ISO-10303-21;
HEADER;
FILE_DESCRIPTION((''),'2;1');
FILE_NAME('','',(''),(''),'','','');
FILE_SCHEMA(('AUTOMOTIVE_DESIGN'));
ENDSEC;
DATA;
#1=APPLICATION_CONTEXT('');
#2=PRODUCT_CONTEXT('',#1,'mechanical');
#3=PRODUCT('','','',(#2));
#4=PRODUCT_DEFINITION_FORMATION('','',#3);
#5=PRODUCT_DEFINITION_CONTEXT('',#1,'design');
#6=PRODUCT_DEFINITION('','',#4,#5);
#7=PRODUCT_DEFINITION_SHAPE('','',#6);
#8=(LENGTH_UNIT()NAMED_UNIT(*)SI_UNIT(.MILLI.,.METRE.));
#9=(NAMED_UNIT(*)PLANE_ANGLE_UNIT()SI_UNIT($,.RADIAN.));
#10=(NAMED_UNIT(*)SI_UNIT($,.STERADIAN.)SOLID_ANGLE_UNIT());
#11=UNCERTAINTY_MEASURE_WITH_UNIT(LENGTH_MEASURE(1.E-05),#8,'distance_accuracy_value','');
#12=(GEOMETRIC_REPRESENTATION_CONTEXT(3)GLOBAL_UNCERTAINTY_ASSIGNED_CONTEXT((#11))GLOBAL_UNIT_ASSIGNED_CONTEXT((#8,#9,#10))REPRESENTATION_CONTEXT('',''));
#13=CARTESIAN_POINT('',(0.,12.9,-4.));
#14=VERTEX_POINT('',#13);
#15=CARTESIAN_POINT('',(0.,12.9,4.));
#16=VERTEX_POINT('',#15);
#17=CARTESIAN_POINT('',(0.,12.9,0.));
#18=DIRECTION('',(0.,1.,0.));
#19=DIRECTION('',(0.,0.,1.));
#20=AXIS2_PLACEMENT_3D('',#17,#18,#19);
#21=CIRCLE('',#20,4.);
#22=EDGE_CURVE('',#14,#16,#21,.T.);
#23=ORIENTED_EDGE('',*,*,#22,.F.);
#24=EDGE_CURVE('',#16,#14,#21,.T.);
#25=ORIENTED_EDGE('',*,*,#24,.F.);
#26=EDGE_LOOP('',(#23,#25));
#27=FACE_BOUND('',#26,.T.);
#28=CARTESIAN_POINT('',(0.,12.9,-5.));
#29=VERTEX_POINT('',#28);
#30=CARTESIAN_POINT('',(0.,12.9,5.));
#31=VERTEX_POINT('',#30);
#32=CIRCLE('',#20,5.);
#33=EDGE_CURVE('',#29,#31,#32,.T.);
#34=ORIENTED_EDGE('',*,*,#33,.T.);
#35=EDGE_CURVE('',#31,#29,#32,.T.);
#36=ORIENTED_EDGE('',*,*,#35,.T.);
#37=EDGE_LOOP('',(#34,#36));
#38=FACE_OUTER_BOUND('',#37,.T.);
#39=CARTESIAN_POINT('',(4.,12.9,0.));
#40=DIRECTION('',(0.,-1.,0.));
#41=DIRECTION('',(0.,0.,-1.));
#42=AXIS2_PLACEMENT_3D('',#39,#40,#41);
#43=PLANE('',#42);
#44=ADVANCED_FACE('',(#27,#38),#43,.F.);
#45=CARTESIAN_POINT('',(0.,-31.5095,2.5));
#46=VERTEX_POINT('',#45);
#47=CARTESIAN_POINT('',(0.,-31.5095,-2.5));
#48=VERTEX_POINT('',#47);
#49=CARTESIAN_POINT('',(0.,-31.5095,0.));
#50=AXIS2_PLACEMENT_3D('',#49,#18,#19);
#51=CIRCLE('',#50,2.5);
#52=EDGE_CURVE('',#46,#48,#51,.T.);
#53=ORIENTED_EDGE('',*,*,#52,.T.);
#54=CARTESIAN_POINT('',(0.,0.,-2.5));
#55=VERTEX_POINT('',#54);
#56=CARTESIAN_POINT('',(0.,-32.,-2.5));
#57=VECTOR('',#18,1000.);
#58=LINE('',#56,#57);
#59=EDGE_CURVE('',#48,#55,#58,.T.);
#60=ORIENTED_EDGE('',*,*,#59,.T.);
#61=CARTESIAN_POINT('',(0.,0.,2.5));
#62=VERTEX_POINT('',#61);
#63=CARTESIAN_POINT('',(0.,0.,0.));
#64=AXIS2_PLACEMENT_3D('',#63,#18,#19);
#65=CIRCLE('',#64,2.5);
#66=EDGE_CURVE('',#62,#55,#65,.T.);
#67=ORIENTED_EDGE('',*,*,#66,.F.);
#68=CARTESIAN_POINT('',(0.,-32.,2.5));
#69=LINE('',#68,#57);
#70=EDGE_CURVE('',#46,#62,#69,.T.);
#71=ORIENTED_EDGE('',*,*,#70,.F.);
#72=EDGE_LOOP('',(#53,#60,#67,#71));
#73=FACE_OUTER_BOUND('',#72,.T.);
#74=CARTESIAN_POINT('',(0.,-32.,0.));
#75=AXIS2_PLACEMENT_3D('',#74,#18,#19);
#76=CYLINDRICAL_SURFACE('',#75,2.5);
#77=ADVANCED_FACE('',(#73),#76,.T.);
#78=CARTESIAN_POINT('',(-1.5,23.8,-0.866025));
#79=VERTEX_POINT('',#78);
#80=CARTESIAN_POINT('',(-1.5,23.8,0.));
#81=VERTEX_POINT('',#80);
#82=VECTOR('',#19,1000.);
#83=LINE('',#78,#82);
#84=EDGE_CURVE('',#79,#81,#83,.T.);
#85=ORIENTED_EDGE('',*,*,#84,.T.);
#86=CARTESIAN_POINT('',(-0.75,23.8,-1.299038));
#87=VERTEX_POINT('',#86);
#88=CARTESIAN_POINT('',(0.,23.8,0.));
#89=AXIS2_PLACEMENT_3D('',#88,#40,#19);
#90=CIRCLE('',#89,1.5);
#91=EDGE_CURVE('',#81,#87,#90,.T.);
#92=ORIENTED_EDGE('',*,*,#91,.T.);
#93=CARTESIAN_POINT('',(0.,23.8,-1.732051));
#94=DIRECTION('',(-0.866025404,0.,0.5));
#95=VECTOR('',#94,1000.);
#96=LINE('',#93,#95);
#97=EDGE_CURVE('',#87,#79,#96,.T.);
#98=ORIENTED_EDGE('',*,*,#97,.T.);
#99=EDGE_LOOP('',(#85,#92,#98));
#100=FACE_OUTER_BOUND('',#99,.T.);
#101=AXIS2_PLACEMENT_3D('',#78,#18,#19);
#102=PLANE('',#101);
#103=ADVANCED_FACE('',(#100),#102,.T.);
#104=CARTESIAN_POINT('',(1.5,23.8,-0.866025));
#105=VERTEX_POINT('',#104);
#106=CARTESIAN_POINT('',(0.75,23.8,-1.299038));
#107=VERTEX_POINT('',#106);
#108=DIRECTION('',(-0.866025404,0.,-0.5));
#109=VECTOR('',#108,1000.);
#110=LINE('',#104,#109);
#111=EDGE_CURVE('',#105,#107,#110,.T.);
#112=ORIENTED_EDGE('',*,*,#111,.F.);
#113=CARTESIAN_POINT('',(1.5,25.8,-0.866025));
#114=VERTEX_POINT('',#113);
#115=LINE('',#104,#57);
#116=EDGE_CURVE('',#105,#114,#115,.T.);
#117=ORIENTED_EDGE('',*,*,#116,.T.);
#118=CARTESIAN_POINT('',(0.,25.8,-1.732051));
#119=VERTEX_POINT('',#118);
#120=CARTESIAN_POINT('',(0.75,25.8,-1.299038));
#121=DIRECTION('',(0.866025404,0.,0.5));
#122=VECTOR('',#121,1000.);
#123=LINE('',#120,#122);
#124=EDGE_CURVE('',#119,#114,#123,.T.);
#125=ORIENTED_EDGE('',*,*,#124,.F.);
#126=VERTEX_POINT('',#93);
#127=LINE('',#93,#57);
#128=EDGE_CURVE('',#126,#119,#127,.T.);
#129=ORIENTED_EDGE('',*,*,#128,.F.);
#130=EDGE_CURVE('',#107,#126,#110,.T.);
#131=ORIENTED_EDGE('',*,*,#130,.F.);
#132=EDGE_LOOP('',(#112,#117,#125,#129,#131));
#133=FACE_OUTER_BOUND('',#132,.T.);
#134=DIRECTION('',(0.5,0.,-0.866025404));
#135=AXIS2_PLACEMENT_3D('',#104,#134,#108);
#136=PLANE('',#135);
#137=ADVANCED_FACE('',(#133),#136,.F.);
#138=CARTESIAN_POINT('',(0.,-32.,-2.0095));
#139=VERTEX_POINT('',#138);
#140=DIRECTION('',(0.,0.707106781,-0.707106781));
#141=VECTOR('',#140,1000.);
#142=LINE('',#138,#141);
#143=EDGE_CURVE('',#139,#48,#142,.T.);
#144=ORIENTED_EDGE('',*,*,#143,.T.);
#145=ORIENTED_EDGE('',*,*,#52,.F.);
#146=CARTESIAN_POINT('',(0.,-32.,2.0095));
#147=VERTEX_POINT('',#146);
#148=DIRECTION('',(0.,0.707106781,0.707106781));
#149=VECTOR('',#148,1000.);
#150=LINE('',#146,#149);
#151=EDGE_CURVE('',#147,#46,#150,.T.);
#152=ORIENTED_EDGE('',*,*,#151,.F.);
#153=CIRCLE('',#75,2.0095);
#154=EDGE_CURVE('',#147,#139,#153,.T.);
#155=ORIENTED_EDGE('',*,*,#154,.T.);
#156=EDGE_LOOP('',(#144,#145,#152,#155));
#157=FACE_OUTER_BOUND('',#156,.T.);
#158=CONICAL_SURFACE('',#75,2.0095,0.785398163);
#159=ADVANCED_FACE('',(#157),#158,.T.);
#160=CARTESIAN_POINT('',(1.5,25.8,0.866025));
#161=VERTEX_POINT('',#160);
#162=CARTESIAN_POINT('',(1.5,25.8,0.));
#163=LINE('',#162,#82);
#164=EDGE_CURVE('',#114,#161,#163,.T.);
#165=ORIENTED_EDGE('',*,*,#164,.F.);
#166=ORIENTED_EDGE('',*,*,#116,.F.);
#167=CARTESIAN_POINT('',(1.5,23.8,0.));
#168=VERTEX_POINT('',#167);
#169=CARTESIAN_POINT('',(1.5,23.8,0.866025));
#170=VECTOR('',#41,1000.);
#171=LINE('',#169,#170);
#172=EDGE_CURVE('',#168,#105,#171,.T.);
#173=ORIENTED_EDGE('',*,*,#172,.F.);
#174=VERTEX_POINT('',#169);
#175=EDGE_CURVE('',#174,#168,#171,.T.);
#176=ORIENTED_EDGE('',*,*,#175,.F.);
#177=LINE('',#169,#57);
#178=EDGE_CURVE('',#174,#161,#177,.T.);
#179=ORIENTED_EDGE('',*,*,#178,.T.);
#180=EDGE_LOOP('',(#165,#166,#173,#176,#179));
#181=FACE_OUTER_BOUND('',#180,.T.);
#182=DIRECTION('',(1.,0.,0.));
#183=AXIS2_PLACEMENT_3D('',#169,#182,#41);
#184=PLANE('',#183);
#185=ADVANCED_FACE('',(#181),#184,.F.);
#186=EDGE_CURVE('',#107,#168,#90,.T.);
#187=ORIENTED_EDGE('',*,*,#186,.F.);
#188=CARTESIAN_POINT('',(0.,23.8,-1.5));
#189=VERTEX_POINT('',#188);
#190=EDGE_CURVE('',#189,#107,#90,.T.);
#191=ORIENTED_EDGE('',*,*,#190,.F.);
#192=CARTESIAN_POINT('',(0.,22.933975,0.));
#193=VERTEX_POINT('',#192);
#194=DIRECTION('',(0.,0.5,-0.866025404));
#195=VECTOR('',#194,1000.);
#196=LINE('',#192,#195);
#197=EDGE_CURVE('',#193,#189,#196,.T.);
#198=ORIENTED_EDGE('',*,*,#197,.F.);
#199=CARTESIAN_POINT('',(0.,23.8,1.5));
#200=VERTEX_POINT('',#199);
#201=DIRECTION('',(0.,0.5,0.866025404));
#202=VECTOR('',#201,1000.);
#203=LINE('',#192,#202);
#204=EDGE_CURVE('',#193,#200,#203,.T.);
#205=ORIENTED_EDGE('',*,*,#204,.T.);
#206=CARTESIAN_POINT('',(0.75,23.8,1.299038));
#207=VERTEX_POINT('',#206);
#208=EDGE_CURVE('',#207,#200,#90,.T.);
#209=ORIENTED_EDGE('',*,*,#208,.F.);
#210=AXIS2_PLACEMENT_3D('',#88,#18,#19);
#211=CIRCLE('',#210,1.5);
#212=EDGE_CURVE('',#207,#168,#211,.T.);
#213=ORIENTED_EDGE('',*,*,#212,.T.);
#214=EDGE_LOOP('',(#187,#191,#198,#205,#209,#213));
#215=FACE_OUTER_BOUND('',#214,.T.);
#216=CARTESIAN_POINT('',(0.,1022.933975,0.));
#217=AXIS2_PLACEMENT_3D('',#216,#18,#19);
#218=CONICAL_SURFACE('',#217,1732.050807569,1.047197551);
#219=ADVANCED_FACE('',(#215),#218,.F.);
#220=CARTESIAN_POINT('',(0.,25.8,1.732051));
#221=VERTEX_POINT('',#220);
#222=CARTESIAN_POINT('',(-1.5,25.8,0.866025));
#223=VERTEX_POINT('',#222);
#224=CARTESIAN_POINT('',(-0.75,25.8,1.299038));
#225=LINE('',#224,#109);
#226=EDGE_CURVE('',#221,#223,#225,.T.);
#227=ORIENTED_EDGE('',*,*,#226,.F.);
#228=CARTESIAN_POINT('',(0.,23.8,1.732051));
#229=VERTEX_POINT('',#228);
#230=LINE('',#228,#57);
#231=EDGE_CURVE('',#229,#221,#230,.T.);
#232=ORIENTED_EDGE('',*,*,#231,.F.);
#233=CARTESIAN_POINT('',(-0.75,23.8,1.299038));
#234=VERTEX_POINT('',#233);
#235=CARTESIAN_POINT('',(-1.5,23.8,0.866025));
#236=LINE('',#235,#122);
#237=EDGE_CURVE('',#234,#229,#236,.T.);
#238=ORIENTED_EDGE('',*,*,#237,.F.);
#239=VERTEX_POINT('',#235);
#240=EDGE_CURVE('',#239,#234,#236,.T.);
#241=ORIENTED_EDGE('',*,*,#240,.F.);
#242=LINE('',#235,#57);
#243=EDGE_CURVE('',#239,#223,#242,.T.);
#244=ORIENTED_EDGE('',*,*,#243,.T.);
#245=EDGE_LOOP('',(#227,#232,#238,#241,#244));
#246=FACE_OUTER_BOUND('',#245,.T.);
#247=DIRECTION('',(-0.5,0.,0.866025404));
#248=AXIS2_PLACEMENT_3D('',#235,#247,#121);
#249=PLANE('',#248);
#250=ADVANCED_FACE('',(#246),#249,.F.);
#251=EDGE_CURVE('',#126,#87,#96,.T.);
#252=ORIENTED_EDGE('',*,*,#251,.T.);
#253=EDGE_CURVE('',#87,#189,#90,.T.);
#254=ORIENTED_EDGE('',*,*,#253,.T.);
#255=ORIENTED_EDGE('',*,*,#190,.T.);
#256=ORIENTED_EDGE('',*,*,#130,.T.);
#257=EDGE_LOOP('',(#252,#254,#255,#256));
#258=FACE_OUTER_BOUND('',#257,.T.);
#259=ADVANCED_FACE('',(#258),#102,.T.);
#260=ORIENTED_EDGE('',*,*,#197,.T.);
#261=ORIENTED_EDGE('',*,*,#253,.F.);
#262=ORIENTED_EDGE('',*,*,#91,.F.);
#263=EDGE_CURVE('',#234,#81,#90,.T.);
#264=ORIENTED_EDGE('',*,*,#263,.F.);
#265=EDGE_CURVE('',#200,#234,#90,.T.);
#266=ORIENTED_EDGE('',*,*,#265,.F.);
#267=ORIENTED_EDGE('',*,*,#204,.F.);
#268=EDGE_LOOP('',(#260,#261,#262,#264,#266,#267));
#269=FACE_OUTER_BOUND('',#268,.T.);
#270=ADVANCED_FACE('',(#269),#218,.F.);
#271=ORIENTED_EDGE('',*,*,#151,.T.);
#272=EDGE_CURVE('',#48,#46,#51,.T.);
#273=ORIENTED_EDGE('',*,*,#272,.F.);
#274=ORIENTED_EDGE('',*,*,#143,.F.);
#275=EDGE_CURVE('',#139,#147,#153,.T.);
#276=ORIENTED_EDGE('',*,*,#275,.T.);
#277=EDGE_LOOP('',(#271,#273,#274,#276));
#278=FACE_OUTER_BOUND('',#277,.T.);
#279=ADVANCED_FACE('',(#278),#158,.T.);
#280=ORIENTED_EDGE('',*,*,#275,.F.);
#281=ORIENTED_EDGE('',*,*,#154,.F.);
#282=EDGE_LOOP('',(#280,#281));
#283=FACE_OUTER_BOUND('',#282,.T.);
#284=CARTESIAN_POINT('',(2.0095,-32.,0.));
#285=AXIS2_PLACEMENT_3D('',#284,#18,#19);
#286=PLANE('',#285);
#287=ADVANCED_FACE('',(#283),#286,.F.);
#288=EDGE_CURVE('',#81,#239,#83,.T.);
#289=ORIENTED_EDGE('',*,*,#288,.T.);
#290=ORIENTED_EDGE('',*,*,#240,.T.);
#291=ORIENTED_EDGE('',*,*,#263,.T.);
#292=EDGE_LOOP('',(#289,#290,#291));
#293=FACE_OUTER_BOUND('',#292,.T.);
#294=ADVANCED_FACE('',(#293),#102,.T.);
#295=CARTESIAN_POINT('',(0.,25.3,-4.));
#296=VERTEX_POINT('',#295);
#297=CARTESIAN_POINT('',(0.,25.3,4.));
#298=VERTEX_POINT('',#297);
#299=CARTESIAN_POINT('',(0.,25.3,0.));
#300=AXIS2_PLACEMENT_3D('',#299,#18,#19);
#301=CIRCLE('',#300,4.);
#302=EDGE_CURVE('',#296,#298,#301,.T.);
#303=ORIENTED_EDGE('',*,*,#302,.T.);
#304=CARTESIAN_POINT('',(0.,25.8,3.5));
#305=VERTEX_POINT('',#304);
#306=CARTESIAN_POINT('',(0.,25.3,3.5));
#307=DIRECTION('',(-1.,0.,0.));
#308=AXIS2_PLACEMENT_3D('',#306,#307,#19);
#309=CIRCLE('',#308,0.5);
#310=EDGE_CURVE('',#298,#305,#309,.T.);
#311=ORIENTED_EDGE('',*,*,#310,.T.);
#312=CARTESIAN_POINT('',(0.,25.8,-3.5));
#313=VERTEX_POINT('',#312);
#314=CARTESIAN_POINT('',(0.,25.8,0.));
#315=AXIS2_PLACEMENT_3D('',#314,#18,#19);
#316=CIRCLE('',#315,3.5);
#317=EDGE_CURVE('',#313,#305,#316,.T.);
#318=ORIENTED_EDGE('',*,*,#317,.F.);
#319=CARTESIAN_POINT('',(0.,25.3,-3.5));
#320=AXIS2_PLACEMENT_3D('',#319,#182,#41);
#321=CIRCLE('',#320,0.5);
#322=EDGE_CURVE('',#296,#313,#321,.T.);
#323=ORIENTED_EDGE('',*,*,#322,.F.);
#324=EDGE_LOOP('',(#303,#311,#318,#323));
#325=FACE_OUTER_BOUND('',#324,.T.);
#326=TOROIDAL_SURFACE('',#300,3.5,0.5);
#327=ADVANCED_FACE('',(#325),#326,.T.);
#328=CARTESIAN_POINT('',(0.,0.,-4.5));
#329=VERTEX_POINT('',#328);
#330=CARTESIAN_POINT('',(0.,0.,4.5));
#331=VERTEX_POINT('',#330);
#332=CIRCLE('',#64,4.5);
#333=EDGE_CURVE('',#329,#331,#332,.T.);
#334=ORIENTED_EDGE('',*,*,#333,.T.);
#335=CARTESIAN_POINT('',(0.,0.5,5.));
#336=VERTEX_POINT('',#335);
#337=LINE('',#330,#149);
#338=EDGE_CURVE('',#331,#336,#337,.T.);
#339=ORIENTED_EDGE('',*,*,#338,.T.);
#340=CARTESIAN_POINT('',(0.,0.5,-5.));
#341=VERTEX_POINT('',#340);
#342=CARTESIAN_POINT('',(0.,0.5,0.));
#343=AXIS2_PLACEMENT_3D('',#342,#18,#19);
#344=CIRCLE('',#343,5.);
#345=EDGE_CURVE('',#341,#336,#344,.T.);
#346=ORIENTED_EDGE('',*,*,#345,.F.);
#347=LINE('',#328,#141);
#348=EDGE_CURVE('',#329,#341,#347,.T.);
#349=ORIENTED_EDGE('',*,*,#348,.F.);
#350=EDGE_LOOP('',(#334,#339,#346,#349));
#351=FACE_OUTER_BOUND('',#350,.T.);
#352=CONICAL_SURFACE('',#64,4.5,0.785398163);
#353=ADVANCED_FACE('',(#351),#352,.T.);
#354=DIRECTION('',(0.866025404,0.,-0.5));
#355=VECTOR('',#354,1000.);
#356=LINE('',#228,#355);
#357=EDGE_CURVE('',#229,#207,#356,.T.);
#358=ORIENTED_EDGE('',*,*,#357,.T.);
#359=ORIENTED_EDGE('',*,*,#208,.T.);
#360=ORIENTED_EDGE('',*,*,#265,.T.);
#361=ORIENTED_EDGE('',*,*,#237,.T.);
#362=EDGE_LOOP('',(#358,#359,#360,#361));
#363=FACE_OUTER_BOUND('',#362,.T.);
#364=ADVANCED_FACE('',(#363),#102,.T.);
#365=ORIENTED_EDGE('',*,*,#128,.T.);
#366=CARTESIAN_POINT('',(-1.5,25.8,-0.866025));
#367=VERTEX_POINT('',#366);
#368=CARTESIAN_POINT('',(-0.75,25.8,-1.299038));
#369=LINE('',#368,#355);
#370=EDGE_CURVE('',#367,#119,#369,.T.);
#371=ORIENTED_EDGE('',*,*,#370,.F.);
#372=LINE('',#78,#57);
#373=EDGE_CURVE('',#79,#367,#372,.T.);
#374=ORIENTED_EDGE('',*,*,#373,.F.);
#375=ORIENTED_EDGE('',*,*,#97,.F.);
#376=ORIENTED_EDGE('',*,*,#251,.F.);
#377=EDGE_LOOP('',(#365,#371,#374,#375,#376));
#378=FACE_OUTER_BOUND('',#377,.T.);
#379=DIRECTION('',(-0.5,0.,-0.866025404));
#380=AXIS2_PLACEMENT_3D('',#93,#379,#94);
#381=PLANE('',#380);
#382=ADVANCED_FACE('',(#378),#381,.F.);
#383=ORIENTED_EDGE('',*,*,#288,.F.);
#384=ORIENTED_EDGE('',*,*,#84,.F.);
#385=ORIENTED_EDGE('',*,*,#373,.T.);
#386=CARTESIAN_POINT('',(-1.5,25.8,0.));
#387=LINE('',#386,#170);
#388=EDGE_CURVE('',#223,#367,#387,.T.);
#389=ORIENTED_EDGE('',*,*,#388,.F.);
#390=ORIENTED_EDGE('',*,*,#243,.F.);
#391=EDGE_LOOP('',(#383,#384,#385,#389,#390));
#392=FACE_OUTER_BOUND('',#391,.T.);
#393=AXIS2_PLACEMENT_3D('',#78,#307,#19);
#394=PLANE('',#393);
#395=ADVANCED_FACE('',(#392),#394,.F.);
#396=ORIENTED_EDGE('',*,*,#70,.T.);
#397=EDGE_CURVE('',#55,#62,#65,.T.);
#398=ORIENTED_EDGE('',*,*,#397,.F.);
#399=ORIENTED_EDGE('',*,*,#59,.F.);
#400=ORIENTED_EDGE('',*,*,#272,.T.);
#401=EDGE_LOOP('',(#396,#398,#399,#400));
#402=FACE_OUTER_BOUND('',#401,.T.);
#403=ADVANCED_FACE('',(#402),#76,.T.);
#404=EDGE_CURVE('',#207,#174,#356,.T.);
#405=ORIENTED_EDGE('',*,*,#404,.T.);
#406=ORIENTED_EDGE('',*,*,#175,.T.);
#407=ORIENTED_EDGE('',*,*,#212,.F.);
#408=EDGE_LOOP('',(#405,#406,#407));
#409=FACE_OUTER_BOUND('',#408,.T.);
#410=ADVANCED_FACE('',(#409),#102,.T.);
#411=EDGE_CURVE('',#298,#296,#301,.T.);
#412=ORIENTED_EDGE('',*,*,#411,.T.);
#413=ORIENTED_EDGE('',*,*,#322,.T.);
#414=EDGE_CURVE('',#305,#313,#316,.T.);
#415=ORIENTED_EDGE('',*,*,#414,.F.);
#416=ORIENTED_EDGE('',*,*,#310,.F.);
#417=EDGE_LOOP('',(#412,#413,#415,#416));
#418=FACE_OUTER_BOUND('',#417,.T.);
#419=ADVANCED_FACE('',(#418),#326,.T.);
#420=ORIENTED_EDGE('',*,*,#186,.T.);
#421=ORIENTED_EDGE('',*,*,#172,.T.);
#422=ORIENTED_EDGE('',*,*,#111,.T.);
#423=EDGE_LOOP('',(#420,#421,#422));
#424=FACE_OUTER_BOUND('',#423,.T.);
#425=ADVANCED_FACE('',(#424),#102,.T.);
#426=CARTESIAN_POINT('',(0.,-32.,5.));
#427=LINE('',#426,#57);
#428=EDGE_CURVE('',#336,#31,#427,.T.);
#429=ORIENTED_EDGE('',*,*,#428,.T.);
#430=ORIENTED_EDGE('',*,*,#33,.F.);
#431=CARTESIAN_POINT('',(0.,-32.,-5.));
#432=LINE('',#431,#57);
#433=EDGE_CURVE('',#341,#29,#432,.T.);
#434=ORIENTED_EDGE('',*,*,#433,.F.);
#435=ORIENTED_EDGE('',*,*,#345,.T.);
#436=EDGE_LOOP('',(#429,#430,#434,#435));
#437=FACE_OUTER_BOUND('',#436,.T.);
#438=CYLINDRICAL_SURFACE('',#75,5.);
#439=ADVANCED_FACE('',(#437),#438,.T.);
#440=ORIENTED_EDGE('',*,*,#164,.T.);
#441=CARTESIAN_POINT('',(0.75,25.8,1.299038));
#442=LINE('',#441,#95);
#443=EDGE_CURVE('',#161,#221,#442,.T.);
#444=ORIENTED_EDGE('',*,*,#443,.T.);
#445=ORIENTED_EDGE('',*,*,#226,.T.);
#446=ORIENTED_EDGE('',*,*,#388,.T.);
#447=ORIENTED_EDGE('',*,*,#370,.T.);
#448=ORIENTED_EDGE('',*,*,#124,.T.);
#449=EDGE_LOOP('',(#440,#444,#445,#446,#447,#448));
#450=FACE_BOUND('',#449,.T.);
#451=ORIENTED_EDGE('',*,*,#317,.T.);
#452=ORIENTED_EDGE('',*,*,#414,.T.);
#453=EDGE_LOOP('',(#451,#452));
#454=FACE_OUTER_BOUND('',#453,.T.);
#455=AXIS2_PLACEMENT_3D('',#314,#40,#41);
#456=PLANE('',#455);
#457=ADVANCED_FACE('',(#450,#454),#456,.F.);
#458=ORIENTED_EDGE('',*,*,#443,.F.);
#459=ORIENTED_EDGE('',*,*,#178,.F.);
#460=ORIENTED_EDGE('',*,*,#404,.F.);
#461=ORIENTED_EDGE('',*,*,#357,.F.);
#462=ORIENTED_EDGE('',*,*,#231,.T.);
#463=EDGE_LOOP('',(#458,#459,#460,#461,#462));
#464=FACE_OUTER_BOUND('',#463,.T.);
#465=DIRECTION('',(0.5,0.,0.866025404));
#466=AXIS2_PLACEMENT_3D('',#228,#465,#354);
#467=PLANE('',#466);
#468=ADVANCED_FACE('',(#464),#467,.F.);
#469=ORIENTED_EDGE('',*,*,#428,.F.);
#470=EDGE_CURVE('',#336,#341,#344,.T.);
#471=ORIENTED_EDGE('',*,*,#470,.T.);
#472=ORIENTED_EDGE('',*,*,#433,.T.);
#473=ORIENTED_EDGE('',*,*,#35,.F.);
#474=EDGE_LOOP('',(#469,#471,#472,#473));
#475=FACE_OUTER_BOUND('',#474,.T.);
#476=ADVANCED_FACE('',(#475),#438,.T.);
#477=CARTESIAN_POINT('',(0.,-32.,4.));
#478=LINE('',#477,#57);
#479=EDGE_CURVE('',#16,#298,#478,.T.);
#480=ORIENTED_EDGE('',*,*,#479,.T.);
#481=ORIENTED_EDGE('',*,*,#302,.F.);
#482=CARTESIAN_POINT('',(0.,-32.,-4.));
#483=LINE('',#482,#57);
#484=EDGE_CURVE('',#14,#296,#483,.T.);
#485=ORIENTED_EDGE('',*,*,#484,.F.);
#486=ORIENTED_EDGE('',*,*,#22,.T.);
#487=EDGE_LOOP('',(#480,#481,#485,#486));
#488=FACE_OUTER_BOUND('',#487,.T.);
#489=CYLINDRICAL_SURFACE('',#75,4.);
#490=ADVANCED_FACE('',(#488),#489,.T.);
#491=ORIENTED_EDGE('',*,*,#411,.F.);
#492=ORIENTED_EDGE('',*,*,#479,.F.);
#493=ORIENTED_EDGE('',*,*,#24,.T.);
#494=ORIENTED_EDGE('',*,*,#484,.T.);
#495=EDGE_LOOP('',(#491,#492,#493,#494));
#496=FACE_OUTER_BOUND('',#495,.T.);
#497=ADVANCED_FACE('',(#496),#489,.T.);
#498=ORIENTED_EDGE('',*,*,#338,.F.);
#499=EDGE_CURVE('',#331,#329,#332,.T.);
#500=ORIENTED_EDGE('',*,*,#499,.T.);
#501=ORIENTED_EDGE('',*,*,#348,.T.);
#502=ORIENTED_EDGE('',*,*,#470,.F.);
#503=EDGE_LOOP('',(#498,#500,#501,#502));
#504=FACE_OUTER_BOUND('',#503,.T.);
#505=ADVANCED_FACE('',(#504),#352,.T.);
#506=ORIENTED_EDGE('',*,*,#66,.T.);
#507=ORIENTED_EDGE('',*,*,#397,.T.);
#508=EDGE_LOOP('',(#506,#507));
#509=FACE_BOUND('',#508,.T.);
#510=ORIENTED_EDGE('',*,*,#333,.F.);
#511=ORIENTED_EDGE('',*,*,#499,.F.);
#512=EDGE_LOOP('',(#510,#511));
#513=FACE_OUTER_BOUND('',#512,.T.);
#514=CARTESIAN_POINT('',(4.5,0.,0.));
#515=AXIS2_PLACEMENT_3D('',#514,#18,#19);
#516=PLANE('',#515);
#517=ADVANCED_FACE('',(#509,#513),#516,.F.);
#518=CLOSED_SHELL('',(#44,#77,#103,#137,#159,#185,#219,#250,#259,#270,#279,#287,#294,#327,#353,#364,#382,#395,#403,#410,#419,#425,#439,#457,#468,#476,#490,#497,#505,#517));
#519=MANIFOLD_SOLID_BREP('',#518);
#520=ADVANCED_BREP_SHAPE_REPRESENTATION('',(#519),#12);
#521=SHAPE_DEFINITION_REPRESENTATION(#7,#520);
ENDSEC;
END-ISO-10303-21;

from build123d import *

# Parameters (mm, degrees)
CUT_EXTRUDE_1_DEPTH      = 2
CUT_EXTRUDE_1_DEPTH_BACK = 2


with BuildPart() as part:
    # 草图1 → 旋转1 (revolve)
    with BuildSketch(Plane.XY, mode=Mode.PRIVATE) as revolve_1_sk:
        with BuildLine():
            Line((0, 25.8), (3.5, 25.8))
            ThreePointArc((3.5, 25.8), (3.853553391, 25.653553391), (4, 25.3))
            Line((4, 25.3), (4, 12.9))
            Line((4, 12.9), (5, 12.9))
            Line((5, 12.9), (5, 0.5))
            Line((5, 0.5), (4.5, 0))
            Line((4.5, 0), (2.5, 0))
            Line((2.5, 0), (2.5, -31.5095))
            Line((2.5, -31.5095), (2.0095, -32))
            Line((2.0095, -32), (0, -32))
            Line((0, -32), (0, 25.8))
        make_face()
    revolve(revolve_1_sk.sketch.rotate(Axis((0, -32, 0), (0, 1, 0)), 270), axis=Axis((0, -32, 0), (0, 1, 0)))

    # 草图2 → 切除-拉伸1 (cut, two sides: drawn at the far end of the back side and taken through both)
    with BuildSketch(Plane(origin=(0, 25.8, 0), x_dir=(-1, 0, 0), z_dir=(0, 1, 0)).offset(-CUT_EXTRUDE_1_DEPTH_BACK)):
        Polygon((1.5, -0.866025404), (1.5, 0.866025404), (0, 1.732050808), (-1.5, 0.866025404), (-1.5, -0.866025404), (0, -1.732050808), align=None)
    extrude(amount=CUT_EXTRUDE_1_DEPTH + CUT_EXTRUDE_1_DEPTH_BACK, mode=Mode.SUBTRACT)

    # 草图3 → 切除-旋转1 (revolve, cut)
    with BuildSketch(Plane.XY, mode=Mode.PRIVATE) as cut_revolve_1_sk:
        Polygon((0, 25.8), (1.5, 25.8), (1.5, 23.8), (0, 22.933974596), align=None)
    revolve(cut_revolve_1_sk.sketch.rotate(Axis((0, 22.933974596, 0), (0, 1, 0)), 270), axis=Axis((0, 22.933974596, 0), (0, 1, 0)), mode=Mode.SUBTRACT)


solid = part.part
